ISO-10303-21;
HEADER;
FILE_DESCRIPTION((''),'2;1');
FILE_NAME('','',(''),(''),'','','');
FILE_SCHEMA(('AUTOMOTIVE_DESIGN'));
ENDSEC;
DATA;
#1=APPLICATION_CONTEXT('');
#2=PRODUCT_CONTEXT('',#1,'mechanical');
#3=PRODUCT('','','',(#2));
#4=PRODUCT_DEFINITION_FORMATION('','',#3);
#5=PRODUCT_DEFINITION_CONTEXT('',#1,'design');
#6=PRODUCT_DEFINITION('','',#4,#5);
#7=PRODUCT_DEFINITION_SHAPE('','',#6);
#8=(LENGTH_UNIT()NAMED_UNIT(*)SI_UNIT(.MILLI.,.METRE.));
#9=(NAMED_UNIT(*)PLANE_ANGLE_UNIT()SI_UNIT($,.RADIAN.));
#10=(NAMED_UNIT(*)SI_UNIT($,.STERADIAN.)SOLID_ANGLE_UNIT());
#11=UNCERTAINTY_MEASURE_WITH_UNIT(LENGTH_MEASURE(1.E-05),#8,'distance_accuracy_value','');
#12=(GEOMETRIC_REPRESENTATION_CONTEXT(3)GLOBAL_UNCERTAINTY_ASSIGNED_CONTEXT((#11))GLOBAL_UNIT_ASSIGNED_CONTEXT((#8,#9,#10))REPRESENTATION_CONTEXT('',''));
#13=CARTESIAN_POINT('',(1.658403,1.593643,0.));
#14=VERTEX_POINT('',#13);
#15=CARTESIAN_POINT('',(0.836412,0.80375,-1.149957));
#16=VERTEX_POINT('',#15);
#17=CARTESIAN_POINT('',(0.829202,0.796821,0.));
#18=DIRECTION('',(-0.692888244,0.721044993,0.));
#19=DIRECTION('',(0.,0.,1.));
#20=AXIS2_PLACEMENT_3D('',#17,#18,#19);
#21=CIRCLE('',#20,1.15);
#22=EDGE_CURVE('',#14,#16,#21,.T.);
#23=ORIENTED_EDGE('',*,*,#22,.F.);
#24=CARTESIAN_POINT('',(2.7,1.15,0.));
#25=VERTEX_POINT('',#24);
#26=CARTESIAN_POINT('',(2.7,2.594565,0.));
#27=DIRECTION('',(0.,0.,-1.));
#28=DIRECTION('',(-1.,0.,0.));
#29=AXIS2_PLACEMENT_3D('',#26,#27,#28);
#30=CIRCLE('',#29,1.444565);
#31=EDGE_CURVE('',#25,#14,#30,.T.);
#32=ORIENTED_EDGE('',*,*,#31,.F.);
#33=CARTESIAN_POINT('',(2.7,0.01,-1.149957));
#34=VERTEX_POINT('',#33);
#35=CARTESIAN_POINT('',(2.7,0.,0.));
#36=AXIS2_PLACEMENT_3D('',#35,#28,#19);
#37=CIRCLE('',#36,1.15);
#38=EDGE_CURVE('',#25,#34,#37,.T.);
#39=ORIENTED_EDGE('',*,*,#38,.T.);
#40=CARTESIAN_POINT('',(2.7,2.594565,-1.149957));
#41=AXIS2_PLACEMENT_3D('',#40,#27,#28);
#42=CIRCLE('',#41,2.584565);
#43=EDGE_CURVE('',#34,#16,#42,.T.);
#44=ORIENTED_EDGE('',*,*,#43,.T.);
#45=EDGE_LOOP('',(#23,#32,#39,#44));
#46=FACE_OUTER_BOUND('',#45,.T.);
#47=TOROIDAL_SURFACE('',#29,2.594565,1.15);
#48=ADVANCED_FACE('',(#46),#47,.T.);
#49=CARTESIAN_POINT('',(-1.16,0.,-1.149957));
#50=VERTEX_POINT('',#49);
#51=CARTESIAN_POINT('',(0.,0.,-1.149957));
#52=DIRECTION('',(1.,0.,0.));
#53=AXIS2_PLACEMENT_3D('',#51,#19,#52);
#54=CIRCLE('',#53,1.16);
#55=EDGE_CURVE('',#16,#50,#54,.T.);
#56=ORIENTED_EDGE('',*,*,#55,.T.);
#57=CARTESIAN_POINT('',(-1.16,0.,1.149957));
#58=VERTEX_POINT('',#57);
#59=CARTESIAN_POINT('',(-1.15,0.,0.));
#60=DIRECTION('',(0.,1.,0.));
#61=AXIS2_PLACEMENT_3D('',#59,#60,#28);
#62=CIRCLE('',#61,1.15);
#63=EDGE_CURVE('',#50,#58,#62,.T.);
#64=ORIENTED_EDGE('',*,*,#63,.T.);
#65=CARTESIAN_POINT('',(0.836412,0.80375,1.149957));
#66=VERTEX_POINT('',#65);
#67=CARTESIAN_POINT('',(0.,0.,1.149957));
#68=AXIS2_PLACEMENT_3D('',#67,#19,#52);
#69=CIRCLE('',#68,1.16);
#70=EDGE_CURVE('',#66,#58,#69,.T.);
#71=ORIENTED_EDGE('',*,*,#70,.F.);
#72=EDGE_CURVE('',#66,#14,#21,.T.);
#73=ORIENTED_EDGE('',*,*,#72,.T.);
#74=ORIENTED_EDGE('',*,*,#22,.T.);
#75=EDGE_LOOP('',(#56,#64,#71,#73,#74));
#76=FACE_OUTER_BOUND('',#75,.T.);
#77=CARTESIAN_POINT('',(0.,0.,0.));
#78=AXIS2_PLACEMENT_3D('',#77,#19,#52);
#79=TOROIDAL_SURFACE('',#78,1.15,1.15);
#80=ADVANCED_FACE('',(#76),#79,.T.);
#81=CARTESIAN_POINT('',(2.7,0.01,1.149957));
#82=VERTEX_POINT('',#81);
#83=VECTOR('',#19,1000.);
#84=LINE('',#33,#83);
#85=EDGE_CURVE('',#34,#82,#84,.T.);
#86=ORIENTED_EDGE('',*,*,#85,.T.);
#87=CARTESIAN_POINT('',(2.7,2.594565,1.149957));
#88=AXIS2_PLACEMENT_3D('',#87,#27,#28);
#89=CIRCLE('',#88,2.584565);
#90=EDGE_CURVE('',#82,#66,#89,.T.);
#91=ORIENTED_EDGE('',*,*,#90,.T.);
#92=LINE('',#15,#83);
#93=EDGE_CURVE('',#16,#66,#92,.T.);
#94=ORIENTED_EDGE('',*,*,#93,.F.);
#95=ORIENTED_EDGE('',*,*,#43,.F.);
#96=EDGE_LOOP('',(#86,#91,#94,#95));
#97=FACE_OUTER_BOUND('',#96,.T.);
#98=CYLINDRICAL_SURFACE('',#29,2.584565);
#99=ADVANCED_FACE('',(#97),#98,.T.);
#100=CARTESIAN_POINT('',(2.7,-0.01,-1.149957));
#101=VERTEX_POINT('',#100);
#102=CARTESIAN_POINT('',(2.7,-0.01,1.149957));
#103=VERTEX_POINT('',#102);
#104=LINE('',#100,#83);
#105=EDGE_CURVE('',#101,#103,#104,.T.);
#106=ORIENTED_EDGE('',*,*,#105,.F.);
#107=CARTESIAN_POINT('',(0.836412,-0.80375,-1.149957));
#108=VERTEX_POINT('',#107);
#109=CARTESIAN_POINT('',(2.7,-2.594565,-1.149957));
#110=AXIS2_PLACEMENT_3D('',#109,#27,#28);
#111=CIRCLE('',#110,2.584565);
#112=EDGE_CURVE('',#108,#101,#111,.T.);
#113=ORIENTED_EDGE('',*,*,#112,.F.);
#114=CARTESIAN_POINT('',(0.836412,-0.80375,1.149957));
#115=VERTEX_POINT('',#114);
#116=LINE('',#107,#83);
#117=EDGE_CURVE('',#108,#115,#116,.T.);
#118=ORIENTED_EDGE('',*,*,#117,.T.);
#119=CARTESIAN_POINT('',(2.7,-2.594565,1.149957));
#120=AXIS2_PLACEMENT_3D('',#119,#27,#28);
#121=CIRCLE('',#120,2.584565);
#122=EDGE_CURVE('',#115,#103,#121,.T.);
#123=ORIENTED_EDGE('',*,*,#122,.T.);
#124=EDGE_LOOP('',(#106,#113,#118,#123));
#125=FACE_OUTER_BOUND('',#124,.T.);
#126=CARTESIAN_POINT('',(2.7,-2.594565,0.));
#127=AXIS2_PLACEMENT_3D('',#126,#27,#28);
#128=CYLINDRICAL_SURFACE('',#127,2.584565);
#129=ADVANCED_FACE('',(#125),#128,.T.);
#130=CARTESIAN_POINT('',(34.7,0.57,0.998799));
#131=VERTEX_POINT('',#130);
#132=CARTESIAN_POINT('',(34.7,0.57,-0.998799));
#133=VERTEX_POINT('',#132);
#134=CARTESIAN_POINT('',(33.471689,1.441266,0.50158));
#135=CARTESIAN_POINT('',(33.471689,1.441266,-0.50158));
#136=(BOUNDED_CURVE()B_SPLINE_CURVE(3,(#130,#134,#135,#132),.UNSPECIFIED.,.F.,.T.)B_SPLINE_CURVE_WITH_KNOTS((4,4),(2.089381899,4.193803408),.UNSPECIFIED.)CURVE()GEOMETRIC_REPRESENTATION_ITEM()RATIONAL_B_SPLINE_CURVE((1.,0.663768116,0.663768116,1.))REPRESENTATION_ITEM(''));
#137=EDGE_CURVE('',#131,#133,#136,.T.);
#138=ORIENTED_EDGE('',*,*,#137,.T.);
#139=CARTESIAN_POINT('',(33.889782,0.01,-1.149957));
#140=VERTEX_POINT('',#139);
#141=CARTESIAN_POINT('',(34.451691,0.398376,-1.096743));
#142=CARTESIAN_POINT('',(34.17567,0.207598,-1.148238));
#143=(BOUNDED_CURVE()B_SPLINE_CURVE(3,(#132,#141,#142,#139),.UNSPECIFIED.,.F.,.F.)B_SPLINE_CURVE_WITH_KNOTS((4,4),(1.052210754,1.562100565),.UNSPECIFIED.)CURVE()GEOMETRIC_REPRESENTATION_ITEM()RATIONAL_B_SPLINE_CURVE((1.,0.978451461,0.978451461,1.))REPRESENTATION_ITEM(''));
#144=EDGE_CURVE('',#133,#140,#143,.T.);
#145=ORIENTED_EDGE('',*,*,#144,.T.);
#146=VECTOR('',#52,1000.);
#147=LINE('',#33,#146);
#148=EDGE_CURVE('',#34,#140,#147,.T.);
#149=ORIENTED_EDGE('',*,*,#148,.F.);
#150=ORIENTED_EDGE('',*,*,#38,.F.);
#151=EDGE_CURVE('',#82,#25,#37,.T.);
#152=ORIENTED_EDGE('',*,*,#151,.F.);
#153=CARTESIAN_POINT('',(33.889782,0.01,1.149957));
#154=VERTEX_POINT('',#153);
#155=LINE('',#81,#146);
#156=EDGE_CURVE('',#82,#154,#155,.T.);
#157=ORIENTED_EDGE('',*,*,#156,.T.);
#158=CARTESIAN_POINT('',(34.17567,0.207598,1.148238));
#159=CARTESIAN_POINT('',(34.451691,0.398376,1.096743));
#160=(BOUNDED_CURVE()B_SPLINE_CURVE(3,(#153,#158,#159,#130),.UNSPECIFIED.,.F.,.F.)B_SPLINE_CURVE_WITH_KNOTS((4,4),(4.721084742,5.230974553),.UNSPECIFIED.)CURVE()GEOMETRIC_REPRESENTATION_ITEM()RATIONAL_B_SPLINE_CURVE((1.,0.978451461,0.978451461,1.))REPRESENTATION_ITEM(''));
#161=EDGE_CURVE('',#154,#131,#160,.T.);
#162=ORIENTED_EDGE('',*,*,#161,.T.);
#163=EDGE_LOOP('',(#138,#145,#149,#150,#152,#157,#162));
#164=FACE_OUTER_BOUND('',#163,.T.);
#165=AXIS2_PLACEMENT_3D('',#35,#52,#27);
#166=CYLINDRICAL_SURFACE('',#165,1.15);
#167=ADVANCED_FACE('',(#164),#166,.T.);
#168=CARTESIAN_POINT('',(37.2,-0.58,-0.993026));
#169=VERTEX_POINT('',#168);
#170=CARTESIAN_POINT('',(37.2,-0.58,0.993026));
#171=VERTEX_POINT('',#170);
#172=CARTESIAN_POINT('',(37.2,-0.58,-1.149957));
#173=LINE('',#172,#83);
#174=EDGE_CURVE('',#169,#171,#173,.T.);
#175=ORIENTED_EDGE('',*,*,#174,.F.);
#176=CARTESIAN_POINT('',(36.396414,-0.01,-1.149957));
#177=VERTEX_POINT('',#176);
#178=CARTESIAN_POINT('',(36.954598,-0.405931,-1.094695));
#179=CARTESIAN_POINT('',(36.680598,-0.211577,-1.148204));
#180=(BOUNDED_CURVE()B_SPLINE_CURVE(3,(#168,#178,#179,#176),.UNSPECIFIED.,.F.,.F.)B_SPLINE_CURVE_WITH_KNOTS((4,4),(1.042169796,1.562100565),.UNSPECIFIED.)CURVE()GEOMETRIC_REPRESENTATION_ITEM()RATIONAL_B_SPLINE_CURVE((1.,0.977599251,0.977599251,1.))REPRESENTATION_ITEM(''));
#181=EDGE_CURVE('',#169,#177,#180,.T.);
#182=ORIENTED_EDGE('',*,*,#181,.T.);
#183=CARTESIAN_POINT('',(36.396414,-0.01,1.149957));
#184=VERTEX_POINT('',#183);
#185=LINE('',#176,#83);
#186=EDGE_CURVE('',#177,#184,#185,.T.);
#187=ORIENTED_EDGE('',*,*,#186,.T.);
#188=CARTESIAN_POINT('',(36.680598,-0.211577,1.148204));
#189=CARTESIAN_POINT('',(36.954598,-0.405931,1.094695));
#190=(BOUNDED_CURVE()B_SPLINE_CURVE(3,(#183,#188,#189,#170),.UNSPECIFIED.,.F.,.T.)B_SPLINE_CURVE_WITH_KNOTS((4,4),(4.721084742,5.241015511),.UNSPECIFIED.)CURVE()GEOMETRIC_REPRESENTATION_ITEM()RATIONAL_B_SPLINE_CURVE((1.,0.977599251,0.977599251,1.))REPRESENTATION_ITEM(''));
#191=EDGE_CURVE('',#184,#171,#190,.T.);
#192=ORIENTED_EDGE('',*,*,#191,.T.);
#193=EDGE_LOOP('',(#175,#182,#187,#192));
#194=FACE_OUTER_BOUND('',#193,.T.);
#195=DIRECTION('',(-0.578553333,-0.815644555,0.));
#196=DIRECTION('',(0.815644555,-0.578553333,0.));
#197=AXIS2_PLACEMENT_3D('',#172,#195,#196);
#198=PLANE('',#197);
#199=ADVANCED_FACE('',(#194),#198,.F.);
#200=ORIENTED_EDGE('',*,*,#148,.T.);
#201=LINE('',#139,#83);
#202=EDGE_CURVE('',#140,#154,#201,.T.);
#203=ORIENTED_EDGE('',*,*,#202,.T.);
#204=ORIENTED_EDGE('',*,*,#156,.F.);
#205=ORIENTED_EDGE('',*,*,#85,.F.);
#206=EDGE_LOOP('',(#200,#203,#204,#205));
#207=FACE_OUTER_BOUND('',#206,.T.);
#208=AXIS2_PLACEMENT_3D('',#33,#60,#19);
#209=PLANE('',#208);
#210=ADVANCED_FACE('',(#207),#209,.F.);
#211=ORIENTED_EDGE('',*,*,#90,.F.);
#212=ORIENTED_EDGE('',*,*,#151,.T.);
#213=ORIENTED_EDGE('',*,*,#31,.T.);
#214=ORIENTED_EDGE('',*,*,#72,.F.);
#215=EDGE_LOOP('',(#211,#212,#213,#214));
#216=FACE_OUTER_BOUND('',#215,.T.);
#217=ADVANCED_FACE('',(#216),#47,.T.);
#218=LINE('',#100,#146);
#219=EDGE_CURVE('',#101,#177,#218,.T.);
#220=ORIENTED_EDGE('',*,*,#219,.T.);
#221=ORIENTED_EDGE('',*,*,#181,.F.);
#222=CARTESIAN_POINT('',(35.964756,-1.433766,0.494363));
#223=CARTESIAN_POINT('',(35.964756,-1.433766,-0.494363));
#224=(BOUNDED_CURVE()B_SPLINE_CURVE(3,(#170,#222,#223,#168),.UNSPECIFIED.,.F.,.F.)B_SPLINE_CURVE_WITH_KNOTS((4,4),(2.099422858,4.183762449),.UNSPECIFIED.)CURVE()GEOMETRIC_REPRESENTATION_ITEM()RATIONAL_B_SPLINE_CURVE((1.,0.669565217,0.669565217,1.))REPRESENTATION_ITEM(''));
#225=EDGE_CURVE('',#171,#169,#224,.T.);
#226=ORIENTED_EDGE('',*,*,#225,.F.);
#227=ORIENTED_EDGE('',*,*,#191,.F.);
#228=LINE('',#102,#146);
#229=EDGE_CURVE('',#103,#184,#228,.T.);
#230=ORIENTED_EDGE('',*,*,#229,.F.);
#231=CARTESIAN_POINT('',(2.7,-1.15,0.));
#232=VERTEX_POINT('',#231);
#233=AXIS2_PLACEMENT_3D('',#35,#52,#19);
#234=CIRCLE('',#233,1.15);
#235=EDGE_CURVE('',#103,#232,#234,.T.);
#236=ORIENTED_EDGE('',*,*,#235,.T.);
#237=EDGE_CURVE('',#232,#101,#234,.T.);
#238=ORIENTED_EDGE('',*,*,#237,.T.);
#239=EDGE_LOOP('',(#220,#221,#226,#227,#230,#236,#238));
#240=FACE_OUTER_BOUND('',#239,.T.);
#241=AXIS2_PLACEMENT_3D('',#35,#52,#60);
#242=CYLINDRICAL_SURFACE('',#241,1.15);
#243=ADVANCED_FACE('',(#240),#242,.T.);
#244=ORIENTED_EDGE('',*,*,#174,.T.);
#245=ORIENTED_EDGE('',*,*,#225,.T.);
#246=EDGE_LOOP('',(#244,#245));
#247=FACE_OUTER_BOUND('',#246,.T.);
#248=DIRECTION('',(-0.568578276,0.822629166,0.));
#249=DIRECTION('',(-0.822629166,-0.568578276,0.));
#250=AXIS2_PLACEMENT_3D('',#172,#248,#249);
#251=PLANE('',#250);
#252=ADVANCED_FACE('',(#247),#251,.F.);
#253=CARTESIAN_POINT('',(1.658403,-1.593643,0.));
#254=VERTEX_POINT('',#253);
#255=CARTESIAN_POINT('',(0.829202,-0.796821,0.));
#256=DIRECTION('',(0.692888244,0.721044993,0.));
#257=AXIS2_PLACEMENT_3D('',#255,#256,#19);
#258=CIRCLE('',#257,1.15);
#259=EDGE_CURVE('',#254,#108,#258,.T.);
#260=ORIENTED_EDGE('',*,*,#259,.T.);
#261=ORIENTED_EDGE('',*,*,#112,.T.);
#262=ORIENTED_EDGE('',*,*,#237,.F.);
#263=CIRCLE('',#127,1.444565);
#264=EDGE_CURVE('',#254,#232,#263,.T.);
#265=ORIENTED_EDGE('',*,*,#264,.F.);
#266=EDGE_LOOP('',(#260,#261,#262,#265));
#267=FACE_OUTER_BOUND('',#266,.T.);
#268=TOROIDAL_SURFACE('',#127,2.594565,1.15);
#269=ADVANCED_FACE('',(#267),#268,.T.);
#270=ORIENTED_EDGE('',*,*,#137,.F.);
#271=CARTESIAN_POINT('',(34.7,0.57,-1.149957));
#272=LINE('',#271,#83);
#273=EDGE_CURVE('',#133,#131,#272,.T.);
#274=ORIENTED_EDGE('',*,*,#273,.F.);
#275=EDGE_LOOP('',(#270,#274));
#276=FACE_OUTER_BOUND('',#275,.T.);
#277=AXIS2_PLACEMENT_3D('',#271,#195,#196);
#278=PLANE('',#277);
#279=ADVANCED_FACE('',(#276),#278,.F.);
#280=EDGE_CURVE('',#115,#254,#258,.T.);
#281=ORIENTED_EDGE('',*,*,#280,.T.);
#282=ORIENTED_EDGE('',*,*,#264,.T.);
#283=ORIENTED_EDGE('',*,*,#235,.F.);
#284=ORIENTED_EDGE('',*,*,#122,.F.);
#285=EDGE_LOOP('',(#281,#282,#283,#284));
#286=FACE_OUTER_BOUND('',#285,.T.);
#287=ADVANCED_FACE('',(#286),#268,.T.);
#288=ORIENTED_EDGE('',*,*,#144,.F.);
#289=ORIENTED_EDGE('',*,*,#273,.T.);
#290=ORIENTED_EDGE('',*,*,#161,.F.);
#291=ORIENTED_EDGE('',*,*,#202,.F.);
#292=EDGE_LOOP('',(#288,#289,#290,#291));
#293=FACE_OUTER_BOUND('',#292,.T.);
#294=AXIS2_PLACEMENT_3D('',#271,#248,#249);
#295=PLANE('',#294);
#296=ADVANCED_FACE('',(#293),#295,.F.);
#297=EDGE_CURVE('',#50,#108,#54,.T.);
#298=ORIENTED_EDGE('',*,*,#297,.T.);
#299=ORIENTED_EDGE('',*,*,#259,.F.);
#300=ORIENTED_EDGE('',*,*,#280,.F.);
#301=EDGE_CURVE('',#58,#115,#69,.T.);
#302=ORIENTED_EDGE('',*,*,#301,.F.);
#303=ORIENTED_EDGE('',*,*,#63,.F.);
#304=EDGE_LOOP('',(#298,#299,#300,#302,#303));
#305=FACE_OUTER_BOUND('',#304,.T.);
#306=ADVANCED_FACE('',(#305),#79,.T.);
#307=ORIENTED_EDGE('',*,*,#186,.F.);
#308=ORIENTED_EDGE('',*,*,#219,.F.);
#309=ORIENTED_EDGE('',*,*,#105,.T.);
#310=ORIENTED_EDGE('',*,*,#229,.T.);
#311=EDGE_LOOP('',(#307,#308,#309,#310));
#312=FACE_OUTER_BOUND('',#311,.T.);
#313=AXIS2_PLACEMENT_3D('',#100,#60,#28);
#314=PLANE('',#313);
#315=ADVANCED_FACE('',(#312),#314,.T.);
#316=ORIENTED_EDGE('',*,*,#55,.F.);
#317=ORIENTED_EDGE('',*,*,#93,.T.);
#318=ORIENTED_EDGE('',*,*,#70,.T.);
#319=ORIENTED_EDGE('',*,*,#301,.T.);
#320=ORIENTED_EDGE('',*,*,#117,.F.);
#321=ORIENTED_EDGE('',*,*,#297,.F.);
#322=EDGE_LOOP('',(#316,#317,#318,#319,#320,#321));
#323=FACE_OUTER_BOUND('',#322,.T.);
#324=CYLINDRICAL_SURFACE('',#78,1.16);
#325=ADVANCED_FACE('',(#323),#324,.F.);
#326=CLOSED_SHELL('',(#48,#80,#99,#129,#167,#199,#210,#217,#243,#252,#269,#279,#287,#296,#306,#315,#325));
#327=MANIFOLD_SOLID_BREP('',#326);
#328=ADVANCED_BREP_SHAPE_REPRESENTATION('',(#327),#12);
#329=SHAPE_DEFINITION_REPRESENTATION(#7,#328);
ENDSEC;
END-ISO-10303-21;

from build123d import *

# Parameters (mm, degrees)
CUT_EXTRUDE1_DEPTH      = 38.288770437
CUT_EXTRUDE1_DEPTH_BACK = 38.288770437


with BuildPart() as part:
    # Sweep2: sweep along a path in Dimension sketch
    with BuildLine(Plane.XY) as sweep2_path:
        Line((34.7, 1.15), (2.7, 1.15))
        ThreePointArc((2.7, 1.15), (2.133929691, 1.265530578), (1.658403483, 1.593642961))
        ThreePointArc((1.658403483, 1.593642961), (-2.3, 0), (1.658403483, -1.593642961))
        ThreePointArc((1.658403483, -1.593642961), (2.133929691, -1.265530578), (2.7, -1.15))
        Line((2.7, -1.15), (37.2, -1.15))
    # Sketch2 → Sweep2 (sweep)
    with BuildSketch(Plane(origin=(34.7, 1.15, 0), x_dir=(0, 0, 1), z_dir=(-1, 0, 0))):
        with BuildLine():
            Line((-1.149956521, -1.14), (1.149956521, -1.14))
            ThreePointArc((1.149956521, -1.14), (0, 0), (-1.149956521, -1.14))
        make_face()
    sweep(path=sweep2_path.line)

    # Sketch3 → Cut-Extrude1 (cut, two sides: drawn at the far end of the back side and taken through both)
    with BuildSketch(Plane.XY.offset(-CUT_EXTRUDE1_DEPTH_BACK)):
        Polygon((34.7, 0.57), (33.882315934, 1.15), (37.21, 1.15), (37.21, -1.15), (36.375313858, -1.15), (37.2, -0.58), (36.382315934, 0), (33.875313858, 0), align=None)
    extrude(amount=CUT_EXTRUDE1_DEPTH + CUT_EXTRUDE1_DEPTH_BACK, mode=Mode.SUBTRACT)


solid = part.part
